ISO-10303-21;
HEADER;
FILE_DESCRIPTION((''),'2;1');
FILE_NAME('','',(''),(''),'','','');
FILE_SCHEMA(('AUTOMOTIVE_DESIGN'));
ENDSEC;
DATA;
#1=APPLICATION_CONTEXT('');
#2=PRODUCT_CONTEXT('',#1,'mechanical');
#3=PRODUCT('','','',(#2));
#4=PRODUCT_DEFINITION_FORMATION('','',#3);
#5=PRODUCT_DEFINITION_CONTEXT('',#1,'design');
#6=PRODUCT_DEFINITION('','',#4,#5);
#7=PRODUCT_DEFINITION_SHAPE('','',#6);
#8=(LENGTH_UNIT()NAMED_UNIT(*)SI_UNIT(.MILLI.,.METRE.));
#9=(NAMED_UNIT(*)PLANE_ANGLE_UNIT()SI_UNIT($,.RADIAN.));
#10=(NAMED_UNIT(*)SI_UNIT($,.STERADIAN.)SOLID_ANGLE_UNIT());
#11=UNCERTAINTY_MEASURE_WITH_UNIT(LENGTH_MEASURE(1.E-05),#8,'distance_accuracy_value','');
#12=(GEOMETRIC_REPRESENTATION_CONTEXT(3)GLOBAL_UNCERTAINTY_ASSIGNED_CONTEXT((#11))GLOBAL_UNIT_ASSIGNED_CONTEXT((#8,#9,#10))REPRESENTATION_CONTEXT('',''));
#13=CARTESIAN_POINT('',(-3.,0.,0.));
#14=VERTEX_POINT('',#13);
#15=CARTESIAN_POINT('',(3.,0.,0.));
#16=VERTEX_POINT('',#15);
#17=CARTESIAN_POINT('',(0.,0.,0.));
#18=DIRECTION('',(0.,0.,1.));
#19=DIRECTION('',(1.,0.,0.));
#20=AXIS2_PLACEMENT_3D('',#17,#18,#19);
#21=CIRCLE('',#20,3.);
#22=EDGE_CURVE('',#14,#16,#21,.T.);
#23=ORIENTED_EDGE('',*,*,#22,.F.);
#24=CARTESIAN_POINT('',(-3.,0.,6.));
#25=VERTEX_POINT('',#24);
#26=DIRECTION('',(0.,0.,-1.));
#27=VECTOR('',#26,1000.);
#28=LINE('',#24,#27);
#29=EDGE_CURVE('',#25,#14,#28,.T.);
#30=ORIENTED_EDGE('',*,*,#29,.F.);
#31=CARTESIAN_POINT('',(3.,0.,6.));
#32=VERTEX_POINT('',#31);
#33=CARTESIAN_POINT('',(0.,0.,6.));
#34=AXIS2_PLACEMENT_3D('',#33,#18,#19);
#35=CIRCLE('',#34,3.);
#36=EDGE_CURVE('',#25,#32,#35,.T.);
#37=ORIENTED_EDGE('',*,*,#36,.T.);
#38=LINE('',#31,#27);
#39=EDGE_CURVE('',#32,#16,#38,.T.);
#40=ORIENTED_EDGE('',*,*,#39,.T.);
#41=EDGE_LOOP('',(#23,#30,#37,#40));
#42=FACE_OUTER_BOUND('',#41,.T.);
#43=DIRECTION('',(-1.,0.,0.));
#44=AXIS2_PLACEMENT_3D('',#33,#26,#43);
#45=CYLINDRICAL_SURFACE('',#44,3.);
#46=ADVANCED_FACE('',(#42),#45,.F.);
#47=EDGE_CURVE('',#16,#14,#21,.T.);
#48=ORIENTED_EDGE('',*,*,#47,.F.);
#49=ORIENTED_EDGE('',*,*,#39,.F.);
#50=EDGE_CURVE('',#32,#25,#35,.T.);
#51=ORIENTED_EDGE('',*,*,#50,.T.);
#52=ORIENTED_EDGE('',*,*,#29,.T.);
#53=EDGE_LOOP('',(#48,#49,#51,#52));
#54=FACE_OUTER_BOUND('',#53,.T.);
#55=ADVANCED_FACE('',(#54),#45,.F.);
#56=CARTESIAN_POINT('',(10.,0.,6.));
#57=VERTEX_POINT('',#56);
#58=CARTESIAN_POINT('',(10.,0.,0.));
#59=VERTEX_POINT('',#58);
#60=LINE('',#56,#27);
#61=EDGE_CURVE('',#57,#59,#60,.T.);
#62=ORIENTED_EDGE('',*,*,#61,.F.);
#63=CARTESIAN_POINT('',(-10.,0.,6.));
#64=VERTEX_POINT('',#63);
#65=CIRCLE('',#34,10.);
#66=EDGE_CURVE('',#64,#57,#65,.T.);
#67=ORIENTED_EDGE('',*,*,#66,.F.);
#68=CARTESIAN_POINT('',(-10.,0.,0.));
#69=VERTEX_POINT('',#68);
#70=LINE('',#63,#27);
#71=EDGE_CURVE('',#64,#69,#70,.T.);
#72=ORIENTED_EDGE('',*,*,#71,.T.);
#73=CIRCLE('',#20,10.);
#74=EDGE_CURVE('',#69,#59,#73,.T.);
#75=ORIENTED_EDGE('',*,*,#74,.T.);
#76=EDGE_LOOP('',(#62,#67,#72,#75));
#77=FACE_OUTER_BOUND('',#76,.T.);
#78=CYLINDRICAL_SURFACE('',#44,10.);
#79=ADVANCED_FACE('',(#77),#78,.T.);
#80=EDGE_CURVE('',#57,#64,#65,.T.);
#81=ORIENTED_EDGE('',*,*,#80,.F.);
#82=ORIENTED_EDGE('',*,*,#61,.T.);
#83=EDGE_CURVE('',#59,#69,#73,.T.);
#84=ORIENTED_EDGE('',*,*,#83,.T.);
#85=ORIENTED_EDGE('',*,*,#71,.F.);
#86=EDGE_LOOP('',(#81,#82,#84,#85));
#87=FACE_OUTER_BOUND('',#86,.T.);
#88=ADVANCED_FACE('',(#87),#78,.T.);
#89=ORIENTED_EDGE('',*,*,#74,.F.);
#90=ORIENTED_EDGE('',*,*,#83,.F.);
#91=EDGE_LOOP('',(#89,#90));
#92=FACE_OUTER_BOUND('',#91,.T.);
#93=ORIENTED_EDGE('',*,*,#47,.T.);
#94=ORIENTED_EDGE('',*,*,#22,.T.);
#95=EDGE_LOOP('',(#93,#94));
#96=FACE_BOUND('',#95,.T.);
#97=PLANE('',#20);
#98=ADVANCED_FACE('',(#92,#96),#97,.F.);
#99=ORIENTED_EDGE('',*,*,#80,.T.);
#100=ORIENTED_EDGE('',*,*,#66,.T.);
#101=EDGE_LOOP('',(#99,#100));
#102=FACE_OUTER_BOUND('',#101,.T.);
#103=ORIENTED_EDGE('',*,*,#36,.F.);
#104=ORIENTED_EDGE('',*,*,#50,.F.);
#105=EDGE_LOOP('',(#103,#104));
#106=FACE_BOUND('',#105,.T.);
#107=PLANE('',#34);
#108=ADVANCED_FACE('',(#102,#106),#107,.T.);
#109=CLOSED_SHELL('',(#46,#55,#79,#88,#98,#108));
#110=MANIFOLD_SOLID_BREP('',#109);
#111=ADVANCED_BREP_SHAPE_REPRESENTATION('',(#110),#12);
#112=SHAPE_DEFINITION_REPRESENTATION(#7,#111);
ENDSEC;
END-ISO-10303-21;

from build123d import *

# Parameters (mm, degrees)
SKETCH1_R           = 10
SKETCH1_R_2         = 3
BOSS_EXTRUDE1_DEPTH = 6


with BuildPart() as part:
    # Sketch1 → Boss-Extrude1 (new body)
    with BuildSketch(Plane.XY):
        Circle(SKETCH1_R)
        Circle(SKETCH1_R_2, mode=Mode.SUBTRACT)
    extrude(amount=BOSS_EXTRUDE1_DEPTH)


solid = part.part
